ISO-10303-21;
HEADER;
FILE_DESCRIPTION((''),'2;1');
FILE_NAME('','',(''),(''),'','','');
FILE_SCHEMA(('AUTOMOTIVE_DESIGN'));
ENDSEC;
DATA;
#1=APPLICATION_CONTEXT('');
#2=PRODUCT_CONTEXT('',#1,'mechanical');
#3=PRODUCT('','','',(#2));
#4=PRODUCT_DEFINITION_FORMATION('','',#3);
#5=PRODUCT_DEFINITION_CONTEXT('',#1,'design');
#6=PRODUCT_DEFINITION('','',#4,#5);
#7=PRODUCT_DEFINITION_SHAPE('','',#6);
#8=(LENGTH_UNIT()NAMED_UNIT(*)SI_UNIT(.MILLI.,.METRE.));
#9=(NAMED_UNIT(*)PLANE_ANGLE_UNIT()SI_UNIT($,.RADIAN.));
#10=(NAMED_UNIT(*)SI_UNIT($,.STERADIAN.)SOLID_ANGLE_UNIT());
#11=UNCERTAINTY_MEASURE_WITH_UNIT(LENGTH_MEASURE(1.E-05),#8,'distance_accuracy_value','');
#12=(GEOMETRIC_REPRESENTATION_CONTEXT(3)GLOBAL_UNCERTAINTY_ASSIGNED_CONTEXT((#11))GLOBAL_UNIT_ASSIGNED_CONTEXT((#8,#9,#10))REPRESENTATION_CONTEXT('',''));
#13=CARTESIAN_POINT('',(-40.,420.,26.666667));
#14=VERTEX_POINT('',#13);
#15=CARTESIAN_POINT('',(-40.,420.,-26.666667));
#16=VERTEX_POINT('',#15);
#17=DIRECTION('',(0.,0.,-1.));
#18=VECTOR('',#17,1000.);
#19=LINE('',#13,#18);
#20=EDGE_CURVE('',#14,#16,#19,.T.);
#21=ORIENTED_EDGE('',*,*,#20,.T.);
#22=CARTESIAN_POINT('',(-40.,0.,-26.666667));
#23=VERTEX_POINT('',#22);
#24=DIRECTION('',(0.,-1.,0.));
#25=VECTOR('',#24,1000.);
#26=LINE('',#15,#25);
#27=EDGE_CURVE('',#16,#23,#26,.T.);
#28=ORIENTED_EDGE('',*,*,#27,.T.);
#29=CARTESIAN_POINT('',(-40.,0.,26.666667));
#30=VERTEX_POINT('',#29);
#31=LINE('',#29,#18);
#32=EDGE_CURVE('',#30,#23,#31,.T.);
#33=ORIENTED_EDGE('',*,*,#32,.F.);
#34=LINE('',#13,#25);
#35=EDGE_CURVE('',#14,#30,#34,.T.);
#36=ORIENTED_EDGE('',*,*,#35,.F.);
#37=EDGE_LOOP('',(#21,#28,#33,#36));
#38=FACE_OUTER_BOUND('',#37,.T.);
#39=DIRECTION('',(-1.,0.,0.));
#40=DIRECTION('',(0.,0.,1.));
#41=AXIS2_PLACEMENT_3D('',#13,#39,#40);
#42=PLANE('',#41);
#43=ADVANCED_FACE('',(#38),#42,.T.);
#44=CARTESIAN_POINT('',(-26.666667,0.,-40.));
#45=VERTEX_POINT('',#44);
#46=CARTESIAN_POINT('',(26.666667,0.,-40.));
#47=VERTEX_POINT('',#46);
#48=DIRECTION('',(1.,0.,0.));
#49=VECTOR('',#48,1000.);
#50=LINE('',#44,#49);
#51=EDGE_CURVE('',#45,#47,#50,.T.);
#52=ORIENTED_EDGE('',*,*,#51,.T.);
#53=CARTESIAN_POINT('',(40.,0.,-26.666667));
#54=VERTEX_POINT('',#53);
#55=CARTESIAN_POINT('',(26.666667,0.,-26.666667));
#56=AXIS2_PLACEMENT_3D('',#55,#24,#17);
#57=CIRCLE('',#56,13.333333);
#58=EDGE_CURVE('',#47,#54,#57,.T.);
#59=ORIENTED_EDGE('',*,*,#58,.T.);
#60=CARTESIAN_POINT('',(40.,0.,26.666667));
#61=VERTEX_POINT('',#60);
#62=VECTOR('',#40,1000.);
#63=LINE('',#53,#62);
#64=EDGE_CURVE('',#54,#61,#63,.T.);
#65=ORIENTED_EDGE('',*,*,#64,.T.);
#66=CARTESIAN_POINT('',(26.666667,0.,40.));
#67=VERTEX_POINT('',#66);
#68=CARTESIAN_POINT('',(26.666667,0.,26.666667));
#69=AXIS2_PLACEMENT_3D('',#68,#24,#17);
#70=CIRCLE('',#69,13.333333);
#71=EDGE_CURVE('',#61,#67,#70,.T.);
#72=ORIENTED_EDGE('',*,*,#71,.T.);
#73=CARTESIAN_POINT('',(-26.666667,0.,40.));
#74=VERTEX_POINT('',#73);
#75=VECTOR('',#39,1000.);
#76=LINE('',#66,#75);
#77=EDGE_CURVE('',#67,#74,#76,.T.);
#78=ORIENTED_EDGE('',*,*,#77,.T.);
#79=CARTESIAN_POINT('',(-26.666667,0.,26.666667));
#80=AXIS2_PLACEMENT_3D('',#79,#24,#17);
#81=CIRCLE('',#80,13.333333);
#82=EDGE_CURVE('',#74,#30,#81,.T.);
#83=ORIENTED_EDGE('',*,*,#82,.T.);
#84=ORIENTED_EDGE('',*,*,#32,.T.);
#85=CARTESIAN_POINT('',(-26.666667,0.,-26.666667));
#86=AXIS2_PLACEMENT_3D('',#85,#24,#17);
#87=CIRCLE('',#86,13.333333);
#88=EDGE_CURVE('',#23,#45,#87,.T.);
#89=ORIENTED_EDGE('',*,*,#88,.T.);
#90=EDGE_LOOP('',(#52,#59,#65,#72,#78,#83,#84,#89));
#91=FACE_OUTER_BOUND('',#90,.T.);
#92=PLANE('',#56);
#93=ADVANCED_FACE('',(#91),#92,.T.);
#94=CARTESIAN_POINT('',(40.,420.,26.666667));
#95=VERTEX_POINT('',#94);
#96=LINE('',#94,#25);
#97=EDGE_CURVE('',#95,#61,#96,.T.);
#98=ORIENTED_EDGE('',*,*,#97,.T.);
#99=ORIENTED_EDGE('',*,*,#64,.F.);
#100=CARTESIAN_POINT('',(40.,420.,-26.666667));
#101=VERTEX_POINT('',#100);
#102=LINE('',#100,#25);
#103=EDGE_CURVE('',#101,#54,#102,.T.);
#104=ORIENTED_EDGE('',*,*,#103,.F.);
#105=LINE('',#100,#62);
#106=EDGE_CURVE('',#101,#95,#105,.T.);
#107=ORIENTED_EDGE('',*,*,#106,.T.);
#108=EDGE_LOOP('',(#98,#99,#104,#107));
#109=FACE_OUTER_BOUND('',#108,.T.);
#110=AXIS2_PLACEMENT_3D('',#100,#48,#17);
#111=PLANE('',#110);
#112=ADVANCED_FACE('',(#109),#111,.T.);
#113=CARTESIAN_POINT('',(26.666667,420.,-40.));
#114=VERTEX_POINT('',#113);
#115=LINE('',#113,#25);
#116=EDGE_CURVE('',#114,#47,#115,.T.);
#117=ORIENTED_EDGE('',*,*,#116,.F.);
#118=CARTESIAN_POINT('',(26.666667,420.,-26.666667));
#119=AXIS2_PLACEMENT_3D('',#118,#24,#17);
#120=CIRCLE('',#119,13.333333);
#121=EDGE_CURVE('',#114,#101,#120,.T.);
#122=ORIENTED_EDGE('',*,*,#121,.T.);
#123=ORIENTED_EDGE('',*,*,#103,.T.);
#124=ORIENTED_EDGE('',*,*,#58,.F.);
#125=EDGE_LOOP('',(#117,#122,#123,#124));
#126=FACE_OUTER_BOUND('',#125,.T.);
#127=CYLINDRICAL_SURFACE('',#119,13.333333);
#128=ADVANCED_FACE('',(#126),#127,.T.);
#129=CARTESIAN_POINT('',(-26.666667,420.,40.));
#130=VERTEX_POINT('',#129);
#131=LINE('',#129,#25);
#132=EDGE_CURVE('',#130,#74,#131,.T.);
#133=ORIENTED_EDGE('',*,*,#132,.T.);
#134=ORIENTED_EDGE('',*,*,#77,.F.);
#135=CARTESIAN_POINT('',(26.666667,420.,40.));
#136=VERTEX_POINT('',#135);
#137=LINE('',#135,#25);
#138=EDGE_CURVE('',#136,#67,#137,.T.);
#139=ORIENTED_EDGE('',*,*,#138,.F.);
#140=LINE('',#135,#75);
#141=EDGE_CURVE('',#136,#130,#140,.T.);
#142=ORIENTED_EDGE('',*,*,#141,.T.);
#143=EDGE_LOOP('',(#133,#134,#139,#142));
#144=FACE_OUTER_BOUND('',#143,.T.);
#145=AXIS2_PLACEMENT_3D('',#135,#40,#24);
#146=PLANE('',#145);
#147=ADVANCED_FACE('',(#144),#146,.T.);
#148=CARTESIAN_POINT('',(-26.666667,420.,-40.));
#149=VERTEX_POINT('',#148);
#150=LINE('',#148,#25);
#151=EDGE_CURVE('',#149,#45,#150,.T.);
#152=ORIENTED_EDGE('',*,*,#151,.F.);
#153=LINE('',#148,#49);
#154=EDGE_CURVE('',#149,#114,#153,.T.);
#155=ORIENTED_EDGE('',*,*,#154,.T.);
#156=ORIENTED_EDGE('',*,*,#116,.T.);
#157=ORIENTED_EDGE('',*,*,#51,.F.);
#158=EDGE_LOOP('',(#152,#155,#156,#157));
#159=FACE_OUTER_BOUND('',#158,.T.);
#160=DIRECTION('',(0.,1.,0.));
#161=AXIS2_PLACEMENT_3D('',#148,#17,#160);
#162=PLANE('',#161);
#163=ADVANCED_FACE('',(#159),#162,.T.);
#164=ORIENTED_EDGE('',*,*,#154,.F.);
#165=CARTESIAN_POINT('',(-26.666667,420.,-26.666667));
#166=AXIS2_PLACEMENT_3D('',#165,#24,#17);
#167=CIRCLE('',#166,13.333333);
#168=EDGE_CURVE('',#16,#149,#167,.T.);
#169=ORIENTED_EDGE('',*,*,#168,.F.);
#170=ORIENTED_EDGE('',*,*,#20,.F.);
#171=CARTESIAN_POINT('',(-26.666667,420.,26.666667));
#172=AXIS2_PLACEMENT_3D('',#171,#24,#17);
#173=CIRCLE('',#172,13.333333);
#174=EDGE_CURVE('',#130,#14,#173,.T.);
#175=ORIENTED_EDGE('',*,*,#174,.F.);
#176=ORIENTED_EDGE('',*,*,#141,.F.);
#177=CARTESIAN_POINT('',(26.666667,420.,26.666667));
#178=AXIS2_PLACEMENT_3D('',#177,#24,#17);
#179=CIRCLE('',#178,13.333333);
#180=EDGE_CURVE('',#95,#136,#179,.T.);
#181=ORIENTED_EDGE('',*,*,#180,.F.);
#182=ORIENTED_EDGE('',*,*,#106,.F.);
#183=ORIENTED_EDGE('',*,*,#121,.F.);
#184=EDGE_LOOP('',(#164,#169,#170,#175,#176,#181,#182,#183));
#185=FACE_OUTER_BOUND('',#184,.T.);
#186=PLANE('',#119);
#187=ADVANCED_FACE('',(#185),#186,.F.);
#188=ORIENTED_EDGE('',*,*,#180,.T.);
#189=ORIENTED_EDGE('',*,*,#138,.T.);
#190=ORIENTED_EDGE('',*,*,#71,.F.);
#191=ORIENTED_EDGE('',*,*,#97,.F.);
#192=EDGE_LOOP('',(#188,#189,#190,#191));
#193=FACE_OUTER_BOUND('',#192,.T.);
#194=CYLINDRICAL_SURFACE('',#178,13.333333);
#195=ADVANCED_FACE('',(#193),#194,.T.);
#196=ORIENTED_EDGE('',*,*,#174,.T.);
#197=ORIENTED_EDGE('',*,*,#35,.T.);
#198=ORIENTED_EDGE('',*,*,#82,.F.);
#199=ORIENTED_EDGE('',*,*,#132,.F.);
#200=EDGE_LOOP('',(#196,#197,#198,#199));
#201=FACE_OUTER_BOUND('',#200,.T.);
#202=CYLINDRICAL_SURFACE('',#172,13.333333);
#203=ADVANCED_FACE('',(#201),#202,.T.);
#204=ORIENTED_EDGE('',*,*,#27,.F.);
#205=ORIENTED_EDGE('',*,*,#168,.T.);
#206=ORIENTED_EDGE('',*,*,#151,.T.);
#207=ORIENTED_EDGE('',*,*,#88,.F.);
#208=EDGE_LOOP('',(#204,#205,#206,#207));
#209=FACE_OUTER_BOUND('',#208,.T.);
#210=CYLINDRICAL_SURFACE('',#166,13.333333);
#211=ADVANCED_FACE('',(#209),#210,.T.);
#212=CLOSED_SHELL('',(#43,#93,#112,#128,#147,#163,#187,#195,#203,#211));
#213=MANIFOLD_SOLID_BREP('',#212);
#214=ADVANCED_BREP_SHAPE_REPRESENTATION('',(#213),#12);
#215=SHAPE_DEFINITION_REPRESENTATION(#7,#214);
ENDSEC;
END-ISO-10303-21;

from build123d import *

# Parameters (mm, degrees)
BOSS_EXTRUDE1_DEPTH = 420


with BuildPart() as part:
    # Sketch1 → Boss-Extrude1 (new body)
    with BuildSketch(Plane.XZ):
        with BuildLine():
            Line((40, -26.666666667), (40, 26.666666667))
            ThreePointArc((40, 26.666666667), (36.094757082, 36.094757082), (26.666666667, 40))
            Line((26.666666667, 40), (-26.666666667, 40))
            ThreePointArc((-26.666666667, 40), (-36.094757082, 36.094757082), (-40, 26.666666667))
            Line((-40, 26.666666667), (-40, -26.666666667))
            ThreePointArc((-40, -26.666666667), (-36.094757082, -36.094757082), (-26.666666667, -40))
            Line((-26.666666667, -40), (26.666666667, -40))
            ThreePointArc((26.666666667, -40), (36.094757082, -36.094757082), (40, -26.666666667))
        make_face()
    extrude(amount=-BOSS_EXTRUDE1_DEPTH)


solid = part.part
